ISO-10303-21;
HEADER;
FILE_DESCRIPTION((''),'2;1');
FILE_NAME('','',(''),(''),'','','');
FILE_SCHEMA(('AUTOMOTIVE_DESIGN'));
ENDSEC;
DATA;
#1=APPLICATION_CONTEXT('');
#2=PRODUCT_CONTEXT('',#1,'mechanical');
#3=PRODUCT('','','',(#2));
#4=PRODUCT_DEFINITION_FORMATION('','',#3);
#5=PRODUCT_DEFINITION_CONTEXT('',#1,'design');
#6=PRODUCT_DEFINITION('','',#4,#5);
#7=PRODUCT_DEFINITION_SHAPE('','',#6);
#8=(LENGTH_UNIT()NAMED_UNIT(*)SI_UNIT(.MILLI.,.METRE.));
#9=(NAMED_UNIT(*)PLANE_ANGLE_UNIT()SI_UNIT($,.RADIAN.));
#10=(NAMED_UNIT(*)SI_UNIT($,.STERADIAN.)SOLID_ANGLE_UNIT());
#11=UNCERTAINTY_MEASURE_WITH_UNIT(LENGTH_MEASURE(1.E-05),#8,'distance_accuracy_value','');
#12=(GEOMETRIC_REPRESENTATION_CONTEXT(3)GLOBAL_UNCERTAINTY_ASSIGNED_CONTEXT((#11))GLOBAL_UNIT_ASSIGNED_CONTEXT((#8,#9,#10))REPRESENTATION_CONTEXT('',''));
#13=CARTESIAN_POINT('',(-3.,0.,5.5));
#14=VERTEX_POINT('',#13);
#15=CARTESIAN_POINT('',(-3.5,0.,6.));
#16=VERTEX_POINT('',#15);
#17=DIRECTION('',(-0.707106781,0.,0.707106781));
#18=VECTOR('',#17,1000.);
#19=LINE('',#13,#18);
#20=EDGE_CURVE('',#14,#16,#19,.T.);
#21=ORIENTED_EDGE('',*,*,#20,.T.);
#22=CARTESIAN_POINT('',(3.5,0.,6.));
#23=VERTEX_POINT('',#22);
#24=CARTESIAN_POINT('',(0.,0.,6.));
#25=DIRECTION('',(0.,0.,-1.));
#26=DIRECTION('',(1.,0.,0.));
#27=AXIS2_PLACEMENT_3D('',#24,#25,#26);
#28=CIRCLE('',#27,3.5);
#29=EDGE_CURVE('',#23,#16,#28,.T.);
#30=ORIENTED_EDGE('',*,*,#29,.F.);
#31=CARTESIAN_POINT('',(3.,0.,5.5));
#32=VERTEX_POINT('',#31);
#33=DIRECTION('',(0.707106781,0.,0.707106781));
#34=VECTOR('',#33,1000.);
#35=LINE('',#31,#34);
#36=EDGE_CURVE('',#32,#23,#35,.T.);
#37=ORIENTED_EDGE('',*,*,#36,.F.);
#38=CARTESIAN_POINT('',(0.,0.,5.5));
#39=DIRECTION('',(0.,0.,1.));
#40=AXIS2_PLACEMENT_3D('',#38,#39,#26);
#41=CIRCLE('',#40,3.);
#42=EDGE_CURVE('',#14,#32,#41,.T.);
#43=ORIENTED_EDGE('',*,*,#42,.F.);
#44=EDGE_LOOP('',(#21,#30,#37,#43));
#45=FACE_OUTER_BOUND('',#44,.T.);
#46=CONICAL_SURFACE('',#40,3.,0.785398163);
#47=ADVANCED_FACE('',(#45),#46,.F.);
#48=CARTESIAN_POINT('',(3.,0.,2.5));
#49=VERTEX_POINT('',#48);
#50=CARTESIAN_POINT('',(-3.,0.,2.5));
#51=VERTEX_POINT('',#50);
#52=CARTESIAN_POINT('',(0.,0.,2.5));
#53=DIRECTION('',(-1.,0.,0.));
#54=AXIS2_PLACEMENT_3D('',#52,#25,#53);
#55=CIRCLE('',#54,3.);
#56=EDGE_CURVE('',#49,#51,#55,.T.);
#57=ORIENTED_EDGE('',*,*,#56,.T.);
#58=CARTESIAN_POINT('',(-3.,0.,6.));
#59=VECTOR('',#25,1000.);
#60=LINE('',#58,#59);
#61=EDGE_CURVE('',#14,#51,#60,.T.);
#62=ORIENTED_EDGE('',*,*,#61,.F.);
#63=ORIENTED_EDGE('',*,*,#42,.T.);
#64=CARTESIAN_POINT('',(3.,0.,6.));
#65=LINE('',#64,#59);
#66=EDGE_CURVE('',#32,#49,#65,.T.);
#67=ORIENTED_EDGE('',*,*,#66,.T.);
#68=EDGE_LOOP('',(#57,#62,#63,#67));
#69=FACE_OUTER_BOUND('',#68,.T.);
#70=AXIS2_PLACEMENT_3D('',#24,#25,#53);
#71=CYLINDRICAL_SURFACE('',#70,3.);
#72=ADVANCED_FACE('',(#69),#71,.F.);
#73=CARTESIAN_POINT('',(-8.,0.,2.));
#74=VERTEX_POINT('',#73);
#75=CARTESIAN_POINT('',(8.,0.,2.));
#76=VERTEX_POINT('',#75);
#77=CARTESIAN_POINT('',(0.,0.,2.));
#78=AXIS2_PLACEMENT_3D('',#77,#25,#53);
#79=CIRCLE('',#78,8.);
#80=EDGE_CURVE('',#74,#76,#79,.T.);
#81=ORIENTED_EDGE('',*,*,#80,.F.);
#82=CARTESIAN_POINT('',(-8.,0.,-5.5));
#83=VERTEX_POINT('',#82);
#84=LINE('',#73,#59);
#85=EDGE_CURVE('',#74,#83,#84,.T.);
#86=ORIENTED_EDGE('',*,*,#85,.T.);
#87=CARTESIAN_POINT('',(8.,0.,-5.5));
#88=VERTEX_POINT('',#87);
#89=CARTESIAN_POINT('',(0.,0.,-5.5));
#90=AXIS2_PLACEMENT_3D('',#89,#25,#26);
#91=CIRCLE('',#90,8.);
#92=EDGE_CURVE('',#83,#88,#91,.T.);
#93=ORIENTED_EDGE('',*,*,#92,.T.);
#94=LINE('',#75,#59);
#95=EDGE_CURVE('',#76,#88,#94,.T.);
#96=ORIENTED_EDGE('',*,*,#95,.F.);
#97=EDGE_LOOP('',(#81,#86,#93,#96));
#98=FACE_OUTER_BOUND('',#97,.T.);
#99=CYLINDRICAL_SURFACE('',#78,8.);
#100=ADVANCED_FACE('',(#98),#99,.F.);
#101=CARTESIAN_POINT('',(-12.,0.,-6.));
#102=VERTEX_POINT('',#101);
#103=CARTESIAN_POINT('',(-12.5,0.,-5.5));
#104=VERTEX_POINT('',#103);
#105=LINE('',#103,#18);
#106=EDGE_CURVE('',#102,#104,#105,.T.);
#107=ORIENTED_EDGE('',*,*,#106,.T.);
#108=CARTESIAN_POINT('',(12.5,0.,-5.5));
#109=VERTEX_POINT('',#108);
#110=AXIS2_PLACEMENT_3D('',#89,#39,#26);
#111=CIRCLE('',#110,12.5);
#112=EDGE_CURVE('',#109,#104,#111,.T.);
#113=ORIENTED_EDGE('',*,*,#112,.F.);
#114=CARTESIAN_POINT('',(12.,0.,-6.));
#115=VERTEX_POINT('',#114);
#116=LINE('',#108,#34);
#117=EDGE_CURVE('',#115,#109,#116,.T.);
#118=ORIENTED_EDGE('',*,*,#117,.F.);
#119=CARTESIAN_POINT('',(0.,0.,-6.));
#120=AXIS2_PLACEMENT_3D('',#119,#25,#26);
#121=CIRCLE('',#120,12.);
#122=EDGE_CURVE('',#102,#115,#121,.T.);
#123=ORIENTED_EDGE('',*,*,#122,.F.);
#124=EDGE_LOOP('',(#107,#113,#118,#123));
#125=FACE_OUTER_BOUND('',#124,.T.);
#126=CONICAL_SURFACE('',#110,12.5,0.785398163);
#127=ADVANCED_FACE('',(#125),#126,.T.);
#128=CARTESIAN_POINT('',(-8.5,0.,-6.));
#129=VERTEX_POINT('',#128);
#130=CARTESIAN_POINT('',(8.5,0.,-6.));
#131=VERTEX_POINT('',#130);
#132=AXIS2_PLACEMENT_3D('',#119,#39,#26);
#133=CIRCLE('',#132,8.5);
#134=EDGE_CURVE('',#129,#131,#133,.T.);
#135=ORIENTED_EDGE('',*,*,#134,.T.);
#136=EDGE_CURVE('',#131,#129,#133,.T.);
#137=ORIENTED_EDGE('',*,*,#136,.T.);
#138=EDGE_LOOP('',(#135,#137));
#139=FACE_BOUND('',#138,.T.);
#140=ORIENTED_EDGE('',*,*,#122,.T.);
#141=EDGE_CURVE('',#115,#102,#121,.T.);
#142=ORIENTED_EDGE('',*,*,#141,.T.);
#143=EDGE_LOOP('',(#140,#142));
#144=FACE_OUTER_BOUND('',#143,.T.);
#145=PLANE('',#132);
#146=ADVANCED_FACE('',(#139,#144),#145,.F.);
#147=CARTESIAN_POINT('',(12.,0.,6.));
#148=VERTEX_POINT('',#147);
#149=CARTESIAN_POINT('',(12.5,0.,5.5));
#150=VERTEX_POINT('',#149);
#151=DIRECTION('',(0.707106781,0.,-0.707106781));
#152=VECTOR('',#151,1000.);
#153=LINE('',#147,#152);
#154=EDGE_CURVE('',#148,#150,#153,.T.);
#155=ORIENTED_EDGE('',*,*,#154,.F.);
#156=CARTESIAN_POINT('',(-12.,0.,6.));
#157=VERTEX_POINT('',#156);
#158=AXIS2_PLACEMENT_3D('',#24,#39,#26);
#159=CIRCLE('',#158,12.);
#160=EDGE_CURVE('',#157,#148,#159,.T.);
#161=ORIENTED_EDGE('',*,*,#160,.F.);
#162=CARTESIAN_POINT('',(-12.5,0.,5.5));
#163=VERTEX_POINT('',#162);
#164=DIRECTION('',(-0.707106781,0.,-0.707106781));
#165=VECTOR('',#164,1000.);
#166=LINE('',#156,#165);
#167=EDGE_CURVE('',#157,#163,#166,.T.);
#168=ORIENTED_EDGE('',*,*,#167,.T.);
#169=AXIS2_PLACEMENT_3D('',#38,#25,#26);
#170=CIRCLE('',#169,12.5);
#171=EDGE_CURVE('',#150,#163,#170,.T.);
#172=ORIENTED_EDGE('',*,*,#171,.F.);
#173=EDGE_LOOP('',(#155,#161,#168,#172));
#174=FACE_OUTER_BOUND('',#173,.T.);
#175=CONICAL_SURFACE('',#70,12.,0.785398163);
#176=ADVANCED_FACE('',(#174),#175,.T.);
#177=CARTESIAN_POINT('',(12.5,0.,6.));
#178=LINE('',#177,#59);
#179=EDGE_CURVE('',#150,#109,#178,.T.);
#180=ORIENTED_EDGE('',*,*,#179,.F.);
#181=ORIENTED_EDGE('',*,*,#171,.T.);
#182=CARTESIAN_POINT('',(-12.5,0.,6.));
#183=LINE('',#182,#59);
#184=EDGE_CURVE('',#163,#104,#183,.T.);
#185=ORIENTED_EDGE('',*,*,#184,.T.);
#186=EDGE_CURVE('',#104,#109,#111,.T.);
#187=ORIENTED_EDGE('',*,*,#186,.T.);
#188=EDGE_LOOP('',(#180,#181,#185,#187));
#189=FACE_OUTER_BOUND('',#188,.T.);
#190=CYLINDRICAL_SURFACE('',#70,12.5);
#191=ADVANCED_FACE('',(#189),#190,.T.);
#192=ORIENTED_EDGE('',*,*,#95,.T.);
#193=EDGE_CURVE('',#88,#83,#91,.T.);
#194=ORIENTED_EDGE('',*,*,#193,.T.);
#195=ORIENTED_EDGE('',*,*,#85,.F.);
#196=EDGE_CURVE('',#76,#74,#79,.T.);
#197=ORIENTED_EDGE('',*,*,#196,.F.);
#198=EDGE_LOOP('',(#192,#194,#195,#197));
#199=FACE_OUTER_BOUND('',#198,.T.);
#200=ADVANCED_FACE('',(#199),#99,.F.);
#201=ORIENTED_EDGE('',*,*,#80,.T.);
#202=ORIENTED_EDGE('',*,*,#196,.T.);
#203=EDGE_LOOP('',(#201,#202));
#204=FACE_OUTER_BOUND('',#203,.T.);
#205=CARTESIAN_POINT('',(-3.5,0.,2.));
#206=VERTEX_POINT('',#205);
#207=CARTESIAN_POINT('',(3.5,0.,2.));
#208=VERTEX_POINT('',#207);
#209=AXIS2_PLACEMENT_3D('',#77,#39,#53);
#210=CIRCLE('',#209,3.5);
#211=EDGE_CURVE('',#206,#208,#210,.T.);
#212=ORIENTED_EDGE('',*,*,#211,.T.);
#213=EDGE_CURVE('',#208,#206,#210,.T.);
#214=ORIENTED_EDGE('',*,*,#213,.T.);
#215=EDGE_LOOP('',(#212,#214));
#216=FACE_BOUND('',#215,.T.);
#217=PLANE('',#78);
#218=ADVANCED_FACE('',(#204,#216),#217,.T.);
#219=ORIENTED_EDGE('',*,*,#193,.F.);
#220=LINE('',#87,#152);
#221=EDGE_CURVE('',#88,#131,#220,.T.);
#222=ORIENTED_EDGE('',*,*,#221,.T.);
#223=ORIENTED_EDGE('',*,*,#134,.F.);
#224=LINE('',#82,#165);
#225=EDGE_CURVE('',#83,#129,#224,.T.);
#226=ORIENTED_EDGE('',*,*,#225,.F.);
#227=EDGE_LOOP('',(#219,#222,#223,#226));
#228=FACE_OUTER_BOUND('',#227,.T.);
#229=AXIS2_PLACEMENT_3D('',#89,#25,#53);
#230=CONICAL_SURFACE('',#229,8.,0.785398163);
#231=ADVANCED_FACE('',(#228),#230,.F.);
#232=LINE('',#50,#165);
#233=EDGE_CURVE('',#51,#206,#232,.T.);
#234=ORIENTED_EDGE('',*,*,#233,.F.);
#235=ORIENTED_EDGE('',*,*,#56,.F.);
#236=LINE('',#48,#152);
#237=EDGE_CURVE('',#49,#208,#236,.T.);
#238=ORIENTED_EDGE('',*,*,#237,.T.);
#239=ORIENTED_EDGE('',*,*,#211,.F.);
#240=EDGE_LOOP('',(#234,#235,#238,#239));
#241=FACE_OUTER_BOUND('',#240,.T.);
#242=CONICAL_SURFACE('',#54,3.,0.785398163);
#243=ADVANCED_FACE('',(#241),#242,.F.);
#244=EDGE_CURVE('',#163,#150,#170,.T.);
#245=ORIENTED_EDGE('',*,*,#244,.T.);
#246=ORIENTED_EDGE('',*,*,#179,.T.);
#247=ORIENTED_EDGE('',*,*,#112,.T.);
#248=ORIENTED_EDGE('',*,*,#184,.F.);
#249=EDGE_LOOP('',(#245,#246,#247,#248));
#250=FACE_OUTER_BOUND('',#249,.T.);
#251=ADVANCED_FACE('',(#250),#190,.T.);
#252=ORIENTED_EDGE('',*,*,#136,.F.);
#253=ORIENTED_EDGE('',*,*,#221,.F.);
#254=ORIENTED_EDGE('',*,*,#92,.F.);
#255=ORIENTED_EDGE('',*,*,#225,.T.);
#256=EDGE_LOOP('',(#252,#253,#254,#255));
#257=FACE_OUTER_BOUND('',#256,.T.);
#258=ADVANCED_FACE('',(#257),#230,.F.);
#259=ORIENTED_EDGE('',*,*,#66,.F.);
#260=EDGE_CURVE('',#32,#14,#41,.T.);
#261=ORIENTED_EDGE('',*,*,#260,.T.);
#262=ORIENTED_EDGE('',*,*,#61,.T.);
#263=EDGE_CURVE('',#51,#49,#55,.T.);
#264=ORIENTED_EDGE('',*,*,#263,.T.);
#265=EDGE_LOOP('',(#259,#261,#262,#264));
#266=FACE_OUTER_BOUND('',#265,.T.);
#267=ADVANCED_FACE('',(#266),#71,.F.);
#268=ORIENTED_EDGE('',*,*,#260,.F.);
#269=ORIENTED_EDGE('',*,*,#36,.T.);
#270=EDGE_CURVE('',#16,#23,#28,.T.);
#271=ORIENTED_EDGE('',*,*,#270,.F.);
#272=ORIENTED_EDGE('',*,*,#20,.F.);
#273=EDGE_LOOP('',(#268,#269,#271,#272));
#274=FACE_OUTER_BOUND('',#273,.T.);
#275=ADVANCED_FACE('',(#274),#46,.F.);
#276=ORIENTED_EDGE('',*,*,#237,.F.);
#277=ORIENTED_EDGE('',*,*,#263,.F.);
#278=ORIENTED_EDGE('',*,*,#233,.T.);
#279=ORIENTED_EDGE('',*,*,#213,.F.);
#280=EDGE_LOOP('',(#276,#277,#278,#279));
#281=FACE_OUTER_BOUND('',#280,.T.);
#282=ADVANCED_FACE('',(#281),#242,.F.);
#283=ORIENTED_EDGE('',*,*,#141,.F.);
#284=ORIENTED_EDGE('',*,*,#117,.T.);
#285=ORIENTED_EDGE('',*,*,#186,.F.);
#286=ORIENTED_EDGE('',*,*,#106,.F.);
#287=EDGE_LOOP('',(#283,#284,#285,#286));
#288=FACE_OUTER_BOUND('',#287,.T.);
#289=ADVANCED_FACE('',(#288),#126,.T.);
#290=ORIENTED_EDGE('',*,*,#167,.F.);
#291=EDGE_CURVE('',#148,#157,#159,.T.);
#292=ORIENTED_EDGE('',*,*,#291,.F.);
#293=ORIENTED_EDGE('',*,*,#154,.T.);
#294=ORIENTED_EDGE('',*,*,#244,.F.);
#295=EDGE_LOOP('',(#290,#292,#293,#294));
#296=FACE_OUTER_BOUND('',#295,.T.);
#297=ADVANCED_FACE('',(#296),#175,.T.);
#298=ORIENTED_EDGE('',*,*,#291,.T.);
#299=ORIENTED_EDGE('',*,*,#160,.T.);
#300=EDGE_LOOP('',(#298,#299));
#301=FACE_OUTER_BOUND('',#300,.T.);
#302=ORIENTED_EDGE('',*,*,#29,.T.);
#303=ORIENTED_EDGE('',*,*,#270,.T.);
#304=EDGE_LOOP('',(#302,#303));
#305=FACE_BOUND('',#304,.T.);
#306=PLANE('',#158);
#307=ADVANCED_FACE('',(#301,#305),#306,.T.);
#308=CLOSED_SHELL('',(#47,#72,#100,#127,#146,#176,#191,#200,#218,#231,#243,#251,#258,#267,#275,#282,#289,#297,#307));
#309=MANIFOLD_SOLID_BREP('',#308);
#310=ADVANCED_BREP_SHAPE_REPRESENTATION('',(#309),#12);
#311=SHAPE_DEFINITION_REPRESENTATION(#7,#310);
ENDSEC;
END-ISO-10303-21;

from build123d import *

# Parameters (mm, degrees)
SKETCH1_R           = 12.5
SKETCH1_R_2         = 3
BOSS_EXTRUDE1_DEPTH = 6
SKETCH2_R           = 8
CUT_EXTRUDE1_DEPTH  = 8
CHAMFER1_SIZE       = 0.5


with BuildPart() as part:
    # Sketch1 → Boss-Extrude1 (new, symmetric)
    with BuildSketch(Plane.XY):
        Circle(SKETCH1_R)
        Circle(SKETCH1_R_2, mode=Mode.SUBTRACT)
    extrude(amount=BOSS_EXTRUDE1_DEPTH, both=True)

    # Sketch2 → Cut-Extrude1 (cut)
    with BuildSketch(Plane(origin=(0, 0, -6), x_dir=(-1, 0, 0), z_dir=(0, 0, -1))):
        Circle(SKETCH2_R)
    extrude(amount=-CUT_EXTRUDE1_DEPTH, mode=Mode.SUBTRACT)

    # Chamfer1
    chamfer1_edges = [part.edges().sort_by_distance(p)[0] for p in [
        (-3, 0, 2),
        (8, 0, -6),
        (-12.5, 0, -6),
        (-12.5, 0, 6),
        (-3, 0, 6),
    ]]
    chamfer(chamfer1_edges, length=CHAMFER1_SIZE)


solid = part.part
